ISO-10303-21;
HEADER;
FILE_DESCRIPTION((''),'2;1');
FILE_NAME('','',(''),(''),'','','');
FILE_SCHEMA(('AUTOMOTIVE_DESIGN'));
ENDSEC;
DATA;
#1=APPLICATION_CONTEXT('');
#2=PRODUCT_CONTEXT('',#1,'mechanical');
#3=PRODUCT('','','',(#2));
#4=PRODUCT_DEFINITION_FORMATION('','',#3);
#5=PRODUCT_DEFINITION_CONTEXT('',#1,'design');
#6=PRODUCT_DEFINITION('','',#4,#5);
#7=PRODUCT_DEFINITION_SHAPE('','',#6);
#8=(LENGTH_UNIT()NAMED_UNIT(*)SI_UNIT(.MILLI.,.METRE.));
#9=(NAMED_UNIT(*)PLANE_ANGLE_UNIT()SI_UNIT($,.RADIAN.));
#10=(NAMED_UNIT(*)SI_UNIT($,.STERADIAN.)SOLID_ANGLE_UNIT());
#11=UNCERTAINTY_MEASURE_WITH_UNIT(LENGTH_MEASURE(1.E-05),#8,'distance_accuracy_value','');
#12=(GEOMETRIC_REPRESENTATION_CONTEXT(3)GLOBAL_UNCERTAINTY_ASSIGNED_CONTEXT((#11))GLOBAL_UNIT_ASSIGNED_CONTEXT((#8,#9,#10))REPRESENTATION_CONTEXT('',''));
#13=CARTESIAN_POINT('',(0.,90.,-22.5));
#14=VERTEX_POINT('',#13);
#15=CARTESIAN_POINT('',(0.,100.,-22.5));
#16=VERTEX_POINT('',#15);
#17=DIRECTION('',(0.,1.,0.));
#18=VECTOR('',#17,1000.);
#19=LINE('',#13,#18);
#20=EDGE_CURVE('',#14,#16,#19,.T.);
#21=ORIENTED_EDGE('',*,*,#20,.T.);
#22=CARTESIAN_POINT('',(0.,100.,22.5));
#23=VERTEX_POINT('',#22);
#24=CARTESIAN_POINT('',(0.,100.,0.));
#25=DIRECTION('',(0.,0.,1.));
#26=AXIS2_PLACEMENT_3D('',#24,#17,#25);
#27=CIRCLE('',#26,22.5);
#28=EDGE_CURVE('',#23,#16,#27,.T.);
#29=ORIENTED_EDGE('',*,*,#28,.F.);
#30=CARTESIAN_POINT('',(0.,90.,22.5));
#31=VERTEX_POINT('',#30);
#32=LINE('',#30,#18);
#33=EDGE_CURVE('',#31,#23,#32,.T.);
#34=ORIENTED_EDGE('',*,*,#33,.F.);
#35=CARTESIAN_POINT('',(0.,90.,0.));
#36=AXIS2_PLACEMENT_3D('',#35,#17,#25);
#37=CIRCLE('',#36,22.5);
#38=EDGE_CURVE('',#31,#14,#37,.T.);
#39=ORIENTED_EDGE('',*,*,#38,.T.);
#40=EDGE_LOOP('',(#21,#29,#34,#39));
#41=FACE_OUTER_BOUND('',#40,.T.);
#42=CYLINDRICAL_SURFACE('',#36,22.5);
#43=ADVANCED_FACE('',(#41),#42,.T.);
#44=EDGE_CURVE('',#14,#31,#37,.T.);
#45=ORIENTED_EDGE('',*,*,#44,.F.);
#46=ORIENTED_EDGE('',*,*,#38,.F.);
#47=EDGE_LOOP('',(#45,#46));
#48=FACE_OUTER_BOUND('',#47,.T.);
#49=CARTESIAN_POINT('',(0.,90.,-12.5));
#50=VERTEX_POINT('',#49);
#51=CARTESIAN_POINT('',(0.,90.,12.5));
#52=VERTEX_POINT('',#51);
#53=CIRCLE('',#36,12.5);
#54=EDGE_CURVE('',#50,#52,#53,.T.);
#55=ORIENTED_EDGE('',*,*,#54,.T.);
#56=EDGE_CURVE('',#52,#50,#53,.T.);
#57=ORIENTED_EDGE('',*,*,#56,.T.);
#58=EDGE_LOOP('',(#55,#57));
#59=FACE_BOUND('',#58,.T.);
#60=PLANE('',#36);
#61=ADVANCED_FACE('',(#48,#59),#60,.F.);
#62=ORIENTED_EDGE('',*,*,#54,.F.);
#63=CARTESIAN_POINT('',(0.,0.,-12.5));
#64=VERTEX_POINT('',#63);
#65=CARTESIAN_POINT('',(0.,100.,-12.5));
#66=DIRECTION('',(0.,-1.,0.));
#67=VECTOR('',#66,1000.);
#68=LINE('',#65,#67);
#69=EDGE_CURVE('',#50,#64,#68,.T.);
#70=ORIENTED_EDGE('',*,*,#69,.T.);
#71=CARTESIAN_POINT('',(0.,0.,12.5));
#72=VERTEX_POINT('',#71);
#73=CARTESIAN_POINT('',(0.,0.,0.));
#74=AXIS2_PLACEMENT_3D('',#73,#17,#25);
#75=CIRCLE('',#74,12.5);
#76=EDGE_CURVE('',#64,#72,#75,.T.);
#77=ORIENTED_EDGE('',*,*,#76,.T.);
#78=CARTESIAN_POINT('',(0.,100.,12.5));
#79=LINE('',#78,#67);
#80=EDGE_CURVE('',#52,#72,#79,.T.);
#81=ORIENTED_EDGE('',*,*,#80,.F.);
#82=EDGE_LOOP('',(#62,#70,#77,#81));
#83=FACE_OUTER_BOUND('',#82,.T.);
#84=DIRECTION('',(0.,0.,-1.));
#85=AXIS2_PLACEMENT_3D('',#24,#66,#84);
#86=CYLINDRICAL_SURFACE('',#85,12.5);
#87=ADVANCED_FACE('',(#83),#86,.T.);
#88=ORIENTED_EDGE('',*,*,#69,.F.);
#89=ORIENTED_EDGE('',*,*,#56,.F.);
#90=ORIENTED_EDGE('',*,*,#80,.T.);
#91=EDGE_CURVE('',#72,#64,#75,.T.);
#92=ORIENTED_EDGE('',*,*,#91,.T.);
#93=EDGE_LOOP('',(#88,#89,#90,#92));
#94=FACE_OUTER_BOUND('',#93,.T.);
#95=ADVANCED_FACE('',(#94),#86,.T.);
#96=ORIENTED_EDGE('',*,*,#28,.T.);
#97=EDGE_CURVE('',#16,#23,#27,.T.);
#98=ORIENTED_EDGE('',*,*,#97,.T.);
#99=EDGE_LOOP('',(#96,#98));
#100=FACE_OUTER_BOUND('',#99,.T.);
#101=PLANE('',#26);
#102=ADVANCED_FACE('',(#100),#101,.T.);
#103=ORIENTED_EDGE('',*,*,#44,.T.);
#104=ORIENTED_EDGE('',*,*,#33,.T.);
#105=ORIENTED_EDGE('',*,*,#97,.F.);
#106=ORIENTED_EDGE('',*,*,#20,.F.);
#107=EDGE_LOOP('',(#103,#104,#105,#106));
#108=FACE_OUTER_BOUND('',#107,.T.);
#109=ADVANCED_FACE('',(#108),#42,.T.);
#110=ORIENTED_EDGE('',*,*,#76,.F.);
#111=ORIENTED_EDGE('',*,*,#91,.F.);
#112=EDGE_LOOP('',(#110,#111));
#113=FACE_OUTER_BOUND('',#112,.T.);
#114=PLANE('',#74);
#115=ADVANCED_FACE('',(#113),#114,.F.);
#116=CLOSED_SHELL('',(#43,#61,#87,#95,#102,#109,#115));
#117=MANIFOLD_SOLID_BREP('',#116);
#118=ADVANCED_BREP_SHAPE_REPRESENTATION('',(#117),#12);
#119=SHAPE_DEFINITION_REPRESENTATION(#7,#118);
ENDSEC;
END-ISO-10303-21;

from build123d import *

# Parameters (mm, degrees)
SKETCH1_R           = 12.5
BOSS_EXTRUDE1_DEPTH = 100
SKETCH2_R           = 22.5
BOSS_EXTRUDE2_DEPTH = 10


with BuildPart() as part:
    # Sketch1 → Boss-Extrude1 (new body)
    with BuildSketch(Plane(origin=(0, 0, 0), x_dir=(1, 0, 0), z_dir=(0, 1, 0))):
        with Locations(Location((0, 0, 0), (0, 0, 270))):
            Circle(SKETCH1_R)
    extrude(amount=BOSS_EXTRUDE1_DEPTH)

    # Sketch2 → Boss-Extrude2 (add)
    with BuildSketch(Plane(origin=(0, 100, 0), x_dir=(1, 0, 0), z_dir=(0, 1, 0))):
        with Locations(Location((0, 0, 0), (0, 0, 270))):
            Circle(SKETCH2_R)
    extrude(amount=-BOSS_EXTRUDE2_DEPTH)


solid = part.part
